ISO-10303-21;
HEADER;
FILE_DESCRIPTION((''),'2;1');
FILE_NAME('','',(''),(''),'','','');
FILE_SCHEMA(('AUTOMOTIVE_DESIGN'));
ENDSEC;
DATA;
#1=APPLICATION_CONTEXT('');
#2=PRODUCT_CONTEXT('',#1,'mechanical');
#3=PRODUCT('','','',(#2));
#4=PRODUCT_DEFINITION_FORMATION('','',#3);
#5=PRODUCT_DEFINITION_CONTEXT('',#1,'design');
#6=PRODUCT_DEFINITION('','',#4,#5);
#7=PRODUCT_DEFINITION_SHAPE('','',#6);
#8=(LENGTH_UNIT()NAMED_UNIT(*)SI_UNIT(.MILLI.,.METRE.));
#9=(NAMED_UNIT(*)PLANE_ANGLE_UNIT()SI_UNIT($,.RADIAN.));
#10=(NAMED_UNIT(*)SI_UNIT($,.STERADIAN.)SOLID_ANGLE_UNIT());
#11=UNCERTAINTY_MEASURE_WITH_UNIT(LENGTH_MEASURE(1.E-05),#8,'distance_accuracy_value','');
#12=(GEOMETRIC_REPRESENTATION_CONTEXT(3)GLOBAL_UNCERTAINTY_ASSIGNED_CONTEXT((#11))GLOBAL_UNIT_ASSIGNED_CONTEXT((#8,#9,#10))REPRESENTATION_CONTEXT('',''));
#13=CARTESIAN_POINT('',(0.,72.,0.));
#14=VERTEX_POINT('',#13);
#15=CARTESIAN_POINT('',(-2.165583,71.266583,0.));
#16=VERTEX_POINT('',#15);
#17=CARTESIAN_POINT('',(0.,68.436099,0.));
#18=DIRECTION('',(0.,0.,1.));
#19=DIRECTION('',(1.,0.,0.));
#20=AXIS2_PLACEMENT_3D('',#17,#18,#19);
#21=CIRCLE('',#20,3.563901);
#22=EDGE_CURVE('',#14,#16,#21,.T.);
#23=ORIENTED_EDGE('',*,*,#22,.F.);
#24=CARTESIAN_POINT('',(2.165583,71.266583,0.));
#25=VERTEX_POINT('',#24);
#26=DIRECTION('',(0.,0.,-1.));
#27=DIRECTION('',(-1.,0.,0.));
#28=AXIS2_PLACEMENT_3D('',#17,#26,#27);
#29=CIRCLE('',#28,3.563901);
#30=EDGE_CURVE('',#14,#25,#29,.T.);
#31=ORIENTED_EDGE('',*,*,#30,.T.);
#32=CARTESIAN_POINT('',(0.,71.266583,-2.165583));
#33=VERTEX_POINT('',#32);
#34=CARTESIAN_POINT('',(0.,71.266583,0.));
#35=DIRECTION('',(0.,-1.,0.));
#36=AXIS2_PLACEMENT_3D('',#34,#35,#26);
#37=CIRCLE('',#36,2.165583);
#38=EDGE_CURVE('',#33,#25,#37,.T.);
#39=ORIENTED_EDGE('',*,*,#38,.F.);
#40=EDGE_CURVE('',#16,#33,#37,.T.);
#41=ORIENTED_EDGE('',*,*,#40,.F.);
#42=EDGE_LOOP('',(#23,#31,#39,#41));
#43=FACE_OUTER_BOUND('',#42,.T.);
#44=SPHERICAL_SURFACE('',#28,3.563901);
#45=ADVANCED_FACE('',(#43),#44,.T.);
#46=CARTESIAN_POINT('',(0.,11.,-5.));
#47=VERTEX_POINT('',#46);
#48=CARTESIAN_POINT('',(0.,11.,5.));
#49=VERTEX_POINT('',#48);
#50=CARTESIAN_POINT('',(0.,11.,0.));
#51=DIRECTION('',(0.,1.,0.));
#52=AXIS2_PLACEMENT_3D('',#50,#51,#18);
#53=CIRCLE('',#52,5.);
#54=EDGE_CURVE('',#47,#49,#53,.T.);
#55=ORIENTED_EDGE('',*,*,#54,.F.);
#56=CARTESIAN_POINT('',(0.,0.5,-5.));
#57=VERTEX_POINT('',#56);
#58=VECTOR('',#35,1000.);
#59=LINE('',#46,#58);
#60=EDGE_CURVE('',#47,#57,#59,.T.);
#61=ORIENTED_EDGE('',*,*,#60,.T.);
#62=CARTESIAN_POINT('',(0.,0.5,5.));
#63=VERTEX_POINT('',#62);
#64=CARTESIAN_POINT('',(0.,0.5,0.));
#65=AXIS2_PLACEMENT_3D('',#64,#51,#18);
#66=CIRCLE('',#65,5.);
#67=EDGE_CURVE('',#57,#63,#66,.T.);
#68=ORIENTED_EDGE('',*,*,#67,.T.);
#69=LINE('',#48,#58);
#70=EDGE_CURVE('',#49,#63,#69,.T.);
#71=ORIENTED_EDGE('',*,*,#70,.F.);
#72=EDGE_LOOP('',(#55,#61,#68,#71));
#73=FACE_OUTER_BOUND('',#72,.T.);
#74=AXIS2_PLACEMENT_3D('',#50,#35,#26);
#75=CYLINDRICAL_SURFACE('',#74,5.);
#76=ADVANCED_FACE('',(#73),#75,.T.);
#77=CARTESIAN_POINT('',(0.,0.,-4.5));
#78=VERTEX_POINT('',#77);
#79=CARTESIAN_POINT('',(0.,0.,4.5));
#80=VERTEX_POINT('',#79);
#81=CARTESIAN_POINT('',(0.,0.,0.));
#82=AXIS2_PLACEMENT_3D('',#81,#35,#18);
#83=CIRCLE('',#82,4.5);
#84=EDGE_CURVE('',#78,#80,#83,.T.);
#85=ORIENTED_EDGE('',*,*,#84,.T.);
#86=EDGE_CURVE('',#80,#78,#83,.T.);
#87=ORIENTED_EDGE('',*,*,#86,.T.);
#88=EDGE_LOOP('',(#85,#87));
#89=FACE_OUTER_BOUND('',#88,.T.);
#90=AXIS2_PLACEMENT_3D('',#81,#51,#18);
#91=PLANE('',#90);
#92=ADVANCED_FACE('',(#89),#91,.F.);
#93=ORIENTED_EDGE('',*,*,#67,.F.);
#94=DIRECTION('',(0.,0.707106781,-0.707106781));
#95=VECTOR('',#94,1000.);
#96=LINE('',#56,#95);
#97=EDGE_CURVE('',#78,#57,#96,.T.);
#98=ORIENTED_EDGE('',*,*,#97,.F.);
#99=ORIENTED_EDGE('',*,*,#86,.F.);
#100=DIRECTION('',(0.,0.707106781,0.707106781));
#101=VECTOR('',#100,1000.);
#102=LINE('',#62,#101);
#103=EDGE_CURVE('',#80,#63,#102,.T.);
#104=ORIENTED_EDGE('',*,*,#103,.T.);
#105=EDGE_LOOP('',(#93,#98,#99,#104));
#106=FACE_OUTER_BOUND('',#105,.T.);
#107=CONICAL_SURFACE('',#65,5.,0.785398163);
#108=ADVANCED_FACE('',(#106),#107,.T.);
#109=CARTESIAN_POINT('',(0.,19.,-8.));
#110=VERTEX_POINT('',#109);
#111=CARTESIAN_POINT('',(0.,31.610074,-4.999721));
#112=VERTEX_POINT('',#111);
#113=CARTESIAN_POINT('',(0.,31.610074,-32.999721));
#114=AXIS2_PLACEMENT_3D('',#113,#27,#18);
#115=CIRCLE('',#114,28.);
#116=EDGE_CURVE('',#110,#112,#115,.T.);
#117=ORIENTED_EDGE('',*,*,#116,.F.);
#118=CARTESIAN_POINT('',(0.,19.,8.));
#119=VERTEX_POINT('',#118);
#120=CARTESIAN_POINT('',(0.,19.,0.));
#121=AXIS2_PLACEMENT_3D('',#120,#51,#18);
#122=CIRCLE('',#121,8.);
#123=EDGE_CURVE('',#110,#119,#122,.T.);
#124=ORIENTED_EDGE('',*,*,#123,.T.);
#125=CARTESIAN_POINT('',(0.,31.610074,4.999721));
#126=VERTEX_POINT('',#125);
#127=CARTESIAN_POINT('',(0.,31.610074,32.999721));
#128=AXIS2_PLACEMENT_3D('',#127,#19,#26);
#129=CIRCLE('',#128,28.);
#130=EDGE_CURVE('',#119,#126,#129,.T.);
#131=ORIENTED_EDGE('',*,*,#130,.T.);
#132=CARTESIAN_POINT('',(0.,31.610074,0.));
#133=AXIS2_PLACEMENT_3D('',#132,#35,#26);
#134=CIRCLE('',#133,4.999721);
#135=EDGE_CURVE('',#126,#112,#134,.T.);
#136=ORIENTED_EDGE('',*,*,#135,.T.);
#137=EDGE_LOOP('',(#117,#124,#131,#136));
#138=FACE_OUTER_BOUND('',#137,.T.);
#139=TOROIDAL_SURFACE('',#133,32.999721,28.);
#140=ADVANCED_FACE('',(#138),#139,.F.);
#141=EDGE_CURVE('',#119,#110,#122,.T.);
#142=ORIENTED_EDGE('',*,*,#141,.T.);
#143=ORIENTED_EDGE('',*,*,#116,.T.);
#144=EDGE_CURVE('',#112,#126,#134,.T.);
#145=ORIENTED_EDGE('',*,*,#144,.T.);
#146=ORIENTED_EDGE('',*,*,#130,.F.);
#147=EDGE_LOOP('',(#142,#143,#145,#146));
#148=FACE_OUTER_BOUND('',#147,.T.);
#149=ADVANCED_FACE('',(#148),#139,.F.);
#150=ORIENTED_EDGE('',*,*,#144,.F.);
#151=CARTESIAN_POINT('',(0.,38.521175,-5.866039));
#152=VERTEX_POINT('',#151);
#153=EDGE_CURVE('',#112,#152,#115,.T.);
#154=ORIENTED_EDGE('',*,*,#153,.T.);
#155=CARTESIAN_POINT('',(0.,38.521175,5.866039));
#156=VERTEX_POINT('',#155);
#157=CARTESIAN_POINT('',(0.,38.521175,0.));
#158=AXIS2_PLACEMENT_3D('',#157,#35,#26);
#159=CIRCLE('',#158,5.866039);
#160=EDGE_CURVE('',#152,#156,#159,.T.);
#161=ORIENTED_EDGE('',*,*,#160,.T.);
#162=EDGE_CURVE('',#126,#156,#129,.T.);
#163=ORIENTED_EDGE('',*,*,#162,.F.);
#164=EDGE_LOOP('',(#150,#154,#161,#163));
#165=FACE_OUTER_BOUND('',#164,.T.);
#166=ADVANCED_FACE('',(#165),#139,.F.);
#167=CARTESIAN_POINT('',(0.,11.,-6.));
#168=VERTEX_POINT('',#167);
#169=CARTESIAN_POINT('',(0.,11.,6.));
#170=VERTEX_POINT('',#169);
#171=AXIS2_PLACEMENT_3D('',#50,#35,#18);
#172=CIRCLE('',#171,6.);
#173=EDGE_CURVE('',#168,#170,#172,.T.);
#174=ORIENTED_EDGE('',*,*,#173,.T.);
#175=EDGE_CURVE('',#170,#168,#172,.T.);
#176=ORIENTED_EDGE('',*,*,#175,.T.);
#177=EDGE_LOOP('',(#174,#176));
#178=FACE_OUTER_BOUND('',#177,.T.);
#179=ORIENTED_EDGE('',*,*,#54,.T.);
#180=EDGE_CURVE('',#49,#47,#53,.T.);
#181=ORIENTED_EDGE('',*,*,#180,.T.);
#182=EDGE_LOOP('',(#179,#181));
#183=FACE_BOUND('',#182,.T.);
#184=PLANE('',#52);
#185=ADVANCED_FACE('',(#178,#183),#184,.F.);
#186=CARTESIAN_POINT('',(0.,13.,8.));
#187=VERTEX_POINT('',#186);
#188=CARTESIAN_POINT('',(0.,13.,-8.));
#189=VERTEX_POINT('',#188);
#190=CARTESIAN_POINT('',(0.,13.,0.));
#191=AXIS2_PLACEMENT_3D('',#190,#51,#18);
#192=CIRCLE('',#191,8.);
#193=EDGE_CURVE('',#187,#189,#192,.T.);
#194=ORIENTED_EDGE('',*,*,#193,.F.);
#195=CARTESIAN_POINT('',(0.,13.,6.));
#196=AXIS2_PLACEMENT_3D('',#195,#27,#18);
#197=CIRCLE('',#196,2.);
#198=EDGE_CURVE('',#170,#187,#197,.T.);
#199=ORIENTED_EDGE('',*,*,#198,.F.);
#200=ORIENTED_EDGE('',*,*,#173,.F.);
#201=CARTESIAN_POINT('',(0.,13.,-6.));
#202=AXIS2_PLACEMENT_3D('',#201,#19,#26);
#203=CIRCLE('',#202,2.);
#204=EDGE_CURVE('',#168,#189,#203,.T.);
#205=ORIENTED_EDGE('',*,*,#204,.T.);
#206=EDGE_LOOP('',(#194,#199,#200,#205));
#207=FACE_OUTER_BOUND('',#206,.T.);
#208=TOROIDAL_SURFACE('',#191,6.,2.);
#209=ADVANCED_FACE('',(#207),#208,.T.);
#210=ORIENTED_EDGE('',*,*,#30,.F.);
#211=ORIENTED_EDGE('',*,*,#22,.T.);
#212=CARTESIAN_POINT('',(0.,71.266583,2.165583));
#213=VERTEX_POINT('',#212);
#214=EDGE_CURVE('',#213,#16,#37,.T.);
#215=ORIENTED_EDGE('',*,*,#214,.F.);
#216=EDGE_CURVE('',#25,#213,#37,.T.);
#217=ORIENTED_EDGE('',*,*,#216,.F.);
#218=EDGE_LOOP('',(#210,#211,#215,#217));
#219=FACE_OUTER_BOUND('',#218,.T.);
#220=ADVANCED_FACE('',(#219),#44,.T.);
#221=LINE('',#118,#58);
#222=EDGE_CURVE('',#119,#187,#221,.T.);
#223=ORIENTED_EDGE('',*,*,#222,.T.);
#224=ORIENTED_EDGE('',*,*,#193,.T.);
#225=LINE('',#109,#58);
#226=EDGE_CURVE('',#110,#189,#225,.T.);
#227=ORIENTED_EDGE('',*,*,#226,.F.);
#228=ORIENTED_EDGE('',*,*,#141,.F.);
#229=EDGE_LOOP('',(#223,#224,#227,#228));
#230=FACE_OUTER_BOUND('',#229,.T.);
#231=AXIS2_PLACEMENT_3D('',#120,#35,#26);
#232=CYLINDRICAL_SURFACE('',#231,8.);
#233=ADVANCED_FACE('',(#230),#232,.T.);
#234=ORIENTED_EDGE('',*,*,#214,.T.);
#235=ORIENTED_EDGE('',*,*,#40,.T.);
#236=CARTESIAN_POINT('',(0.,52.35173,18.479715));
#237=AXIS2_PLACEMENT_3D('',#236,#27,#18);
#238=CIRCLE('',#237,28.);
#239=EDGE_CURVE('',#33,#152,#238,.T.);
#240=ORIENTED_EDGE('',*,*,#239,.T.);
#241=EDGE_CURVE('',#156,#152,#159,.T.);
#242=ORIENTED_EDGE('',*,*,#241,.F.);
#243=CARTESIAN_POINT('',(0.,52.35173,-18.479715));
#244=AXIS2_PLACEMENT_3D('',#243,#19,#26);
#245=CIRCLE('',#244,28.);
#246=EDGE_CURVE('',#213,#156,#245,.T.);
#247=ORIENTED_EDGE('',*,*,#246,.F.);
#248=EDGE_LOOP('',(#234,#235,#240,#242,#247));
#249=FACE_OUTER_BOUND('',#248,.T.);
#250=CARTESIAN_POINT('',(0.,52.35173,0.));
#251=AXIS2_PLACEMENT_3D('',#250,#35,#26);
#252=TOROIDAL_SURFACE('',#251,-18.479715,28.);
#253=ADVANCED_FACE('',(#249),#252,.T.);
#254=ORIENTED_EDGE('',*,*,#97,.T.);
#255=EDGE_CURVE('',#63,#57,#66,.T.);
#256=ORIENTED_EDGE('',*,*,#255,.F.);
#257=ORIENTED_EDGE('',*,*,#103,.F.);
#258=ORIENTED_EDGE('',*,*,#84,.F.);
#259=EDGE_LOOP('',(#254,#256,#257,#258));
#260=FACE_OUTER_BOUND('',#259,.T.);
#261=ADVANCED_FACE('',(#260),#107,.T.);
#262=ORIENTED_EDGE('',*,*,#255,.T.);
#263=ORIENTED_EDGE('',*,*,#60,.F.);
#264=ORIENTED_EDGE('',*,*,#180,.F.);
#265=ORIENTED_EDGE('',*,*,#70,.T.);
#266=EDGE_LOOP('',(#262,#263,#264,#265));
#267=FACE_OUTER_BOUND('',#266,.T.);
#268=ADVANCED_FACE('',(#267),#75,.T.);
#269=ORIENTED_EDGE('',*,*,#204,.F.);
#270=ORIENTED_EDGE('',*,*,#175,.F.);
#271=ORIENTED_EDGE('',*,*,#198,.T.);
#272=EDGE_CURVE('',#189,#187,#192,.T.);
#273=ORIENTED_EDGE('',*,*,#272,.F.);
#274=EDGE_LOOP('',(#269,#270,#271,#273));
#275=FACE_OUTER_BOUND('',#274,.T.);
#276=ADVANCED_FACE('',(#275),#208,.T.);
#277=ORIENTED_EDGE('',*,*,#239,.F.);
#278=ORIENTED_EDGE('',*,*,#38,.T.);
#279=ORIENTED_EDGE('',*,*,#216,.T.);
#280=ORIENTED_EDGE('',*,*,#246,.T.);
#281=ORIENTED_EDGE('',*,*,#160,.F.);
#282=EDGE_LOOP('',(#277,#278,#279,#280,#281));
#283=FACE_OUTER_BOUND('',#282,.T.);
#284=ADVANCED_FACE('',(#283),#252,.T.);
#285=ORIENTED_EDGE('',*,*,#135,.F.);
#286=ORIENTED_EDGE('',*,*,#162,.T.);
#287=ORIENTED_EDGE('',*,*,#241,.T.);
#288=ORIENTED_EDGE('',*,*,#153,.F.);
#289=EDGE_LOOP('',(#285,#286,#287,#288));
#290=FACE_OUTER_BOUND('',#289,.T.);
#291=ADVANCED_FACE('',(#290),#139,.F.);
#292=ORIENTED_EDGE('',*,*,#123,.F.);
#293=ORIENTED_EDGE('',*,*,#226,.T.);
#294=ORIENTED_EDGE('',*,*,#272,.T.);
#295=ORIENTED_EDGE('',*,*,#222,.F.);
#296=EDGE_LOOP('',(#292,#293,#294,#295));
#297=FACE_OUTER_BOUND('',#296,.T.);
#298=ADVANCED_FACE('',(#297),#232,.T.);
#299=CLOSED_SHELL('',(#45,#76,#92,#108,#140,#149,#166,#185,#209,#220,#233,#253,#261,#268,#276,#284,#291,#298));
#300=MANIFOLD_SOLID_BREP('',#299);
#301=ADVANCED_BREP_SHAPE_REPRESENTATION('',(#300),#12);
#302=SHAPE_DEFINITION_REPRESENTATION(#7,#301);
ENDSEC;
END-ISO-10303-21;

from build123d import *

# Parameters (mm, degrees)
SHANK_SKETCH_10_R          = 5
SHANK_10_DEPTH             = 11
SHANK_END_CHAMFER_0_5_SIZE = 0.5
COLLAR_SKETCH_16_R         = 8
COLLAR_16_DEPTH            = 8
COLLAR_FILLET_R2_R         = 2


with BuildPart() as part:
    # Shank Sketch Ø10 → Shank Ø10 (new body)
    with BuildSketch(Plane(origin=(0, 0, 0), x_dir=(1, 0, 0), z_dir=(0, 1, 0))):
        with Locations(Location((0, 0, 0), (0, 0, 270))):
            Circle(SHANK_SKETCH_10_R)
    extrude(amount=SHANK_10_DEPTH)

    # Shank End Chamfer 0.5
    shank_end_chamfer_0_5_edges = [part.edges().sort_by_distance(p)[0] for p in [
        (0, 0, -5),
    ]]
    chamfer(shank_end_chamfer_0_5_edges, length=SHANK_END_CHAMFER_0_5_SIZE)

    # Collar Sketch Ø16 → Collar Ø16 (add)
    with BuildSketch(Plane(origin=(0, 11, 0), x_dir=(1, 0, 0), z_dir=(0, 1, 0))):
        with Locations(Location((0, 0, 0), (0, 0, 270))):
            Circle(COLLAR_SKETCH_16_R)
    extrude(amount=COLLAR_16_DEPTH)

    # Collar Fillet R2
    collar_fillet_r2_edges = [part.edges().sort_by_distance(p)[0] for p in [
        (0, 11, -8),
    ]]
    fillet(collar_fillet_r2_edges, radius=COLLAR_FILLET_R2_R)

    # Grip Profile Sketch → Grip Knob (revolve)
    with BuildSketch(Plane.XY, mode=Mode.PRIVATE) as grip_knob_sk:
        with BuildLine():
            Line((-8, 19), (0, 19))
            Line((0, 19), (0, 72))
            ThreePointArc((0, 72), (-1.143202963, 71.811669668), (-2.165583383, 71.266582881))
            ThreePointArc((-2.165583383, 71.266582881), (-9.343191716, 55.495909404), (-5.86603911, 38.521174854))
            ThreePointArc((-5.86603911, 38.521174854), (-5.165533535, 28.567374361), (-8, 19))
        make_face()
    revolve(grip_knob_sk.sketch.rotate(Axis((0, 0, 0), (0, 1, 0)), 270), axis=Axis((0, 0, 0), (0, 1, 0)))


solid = part.part
